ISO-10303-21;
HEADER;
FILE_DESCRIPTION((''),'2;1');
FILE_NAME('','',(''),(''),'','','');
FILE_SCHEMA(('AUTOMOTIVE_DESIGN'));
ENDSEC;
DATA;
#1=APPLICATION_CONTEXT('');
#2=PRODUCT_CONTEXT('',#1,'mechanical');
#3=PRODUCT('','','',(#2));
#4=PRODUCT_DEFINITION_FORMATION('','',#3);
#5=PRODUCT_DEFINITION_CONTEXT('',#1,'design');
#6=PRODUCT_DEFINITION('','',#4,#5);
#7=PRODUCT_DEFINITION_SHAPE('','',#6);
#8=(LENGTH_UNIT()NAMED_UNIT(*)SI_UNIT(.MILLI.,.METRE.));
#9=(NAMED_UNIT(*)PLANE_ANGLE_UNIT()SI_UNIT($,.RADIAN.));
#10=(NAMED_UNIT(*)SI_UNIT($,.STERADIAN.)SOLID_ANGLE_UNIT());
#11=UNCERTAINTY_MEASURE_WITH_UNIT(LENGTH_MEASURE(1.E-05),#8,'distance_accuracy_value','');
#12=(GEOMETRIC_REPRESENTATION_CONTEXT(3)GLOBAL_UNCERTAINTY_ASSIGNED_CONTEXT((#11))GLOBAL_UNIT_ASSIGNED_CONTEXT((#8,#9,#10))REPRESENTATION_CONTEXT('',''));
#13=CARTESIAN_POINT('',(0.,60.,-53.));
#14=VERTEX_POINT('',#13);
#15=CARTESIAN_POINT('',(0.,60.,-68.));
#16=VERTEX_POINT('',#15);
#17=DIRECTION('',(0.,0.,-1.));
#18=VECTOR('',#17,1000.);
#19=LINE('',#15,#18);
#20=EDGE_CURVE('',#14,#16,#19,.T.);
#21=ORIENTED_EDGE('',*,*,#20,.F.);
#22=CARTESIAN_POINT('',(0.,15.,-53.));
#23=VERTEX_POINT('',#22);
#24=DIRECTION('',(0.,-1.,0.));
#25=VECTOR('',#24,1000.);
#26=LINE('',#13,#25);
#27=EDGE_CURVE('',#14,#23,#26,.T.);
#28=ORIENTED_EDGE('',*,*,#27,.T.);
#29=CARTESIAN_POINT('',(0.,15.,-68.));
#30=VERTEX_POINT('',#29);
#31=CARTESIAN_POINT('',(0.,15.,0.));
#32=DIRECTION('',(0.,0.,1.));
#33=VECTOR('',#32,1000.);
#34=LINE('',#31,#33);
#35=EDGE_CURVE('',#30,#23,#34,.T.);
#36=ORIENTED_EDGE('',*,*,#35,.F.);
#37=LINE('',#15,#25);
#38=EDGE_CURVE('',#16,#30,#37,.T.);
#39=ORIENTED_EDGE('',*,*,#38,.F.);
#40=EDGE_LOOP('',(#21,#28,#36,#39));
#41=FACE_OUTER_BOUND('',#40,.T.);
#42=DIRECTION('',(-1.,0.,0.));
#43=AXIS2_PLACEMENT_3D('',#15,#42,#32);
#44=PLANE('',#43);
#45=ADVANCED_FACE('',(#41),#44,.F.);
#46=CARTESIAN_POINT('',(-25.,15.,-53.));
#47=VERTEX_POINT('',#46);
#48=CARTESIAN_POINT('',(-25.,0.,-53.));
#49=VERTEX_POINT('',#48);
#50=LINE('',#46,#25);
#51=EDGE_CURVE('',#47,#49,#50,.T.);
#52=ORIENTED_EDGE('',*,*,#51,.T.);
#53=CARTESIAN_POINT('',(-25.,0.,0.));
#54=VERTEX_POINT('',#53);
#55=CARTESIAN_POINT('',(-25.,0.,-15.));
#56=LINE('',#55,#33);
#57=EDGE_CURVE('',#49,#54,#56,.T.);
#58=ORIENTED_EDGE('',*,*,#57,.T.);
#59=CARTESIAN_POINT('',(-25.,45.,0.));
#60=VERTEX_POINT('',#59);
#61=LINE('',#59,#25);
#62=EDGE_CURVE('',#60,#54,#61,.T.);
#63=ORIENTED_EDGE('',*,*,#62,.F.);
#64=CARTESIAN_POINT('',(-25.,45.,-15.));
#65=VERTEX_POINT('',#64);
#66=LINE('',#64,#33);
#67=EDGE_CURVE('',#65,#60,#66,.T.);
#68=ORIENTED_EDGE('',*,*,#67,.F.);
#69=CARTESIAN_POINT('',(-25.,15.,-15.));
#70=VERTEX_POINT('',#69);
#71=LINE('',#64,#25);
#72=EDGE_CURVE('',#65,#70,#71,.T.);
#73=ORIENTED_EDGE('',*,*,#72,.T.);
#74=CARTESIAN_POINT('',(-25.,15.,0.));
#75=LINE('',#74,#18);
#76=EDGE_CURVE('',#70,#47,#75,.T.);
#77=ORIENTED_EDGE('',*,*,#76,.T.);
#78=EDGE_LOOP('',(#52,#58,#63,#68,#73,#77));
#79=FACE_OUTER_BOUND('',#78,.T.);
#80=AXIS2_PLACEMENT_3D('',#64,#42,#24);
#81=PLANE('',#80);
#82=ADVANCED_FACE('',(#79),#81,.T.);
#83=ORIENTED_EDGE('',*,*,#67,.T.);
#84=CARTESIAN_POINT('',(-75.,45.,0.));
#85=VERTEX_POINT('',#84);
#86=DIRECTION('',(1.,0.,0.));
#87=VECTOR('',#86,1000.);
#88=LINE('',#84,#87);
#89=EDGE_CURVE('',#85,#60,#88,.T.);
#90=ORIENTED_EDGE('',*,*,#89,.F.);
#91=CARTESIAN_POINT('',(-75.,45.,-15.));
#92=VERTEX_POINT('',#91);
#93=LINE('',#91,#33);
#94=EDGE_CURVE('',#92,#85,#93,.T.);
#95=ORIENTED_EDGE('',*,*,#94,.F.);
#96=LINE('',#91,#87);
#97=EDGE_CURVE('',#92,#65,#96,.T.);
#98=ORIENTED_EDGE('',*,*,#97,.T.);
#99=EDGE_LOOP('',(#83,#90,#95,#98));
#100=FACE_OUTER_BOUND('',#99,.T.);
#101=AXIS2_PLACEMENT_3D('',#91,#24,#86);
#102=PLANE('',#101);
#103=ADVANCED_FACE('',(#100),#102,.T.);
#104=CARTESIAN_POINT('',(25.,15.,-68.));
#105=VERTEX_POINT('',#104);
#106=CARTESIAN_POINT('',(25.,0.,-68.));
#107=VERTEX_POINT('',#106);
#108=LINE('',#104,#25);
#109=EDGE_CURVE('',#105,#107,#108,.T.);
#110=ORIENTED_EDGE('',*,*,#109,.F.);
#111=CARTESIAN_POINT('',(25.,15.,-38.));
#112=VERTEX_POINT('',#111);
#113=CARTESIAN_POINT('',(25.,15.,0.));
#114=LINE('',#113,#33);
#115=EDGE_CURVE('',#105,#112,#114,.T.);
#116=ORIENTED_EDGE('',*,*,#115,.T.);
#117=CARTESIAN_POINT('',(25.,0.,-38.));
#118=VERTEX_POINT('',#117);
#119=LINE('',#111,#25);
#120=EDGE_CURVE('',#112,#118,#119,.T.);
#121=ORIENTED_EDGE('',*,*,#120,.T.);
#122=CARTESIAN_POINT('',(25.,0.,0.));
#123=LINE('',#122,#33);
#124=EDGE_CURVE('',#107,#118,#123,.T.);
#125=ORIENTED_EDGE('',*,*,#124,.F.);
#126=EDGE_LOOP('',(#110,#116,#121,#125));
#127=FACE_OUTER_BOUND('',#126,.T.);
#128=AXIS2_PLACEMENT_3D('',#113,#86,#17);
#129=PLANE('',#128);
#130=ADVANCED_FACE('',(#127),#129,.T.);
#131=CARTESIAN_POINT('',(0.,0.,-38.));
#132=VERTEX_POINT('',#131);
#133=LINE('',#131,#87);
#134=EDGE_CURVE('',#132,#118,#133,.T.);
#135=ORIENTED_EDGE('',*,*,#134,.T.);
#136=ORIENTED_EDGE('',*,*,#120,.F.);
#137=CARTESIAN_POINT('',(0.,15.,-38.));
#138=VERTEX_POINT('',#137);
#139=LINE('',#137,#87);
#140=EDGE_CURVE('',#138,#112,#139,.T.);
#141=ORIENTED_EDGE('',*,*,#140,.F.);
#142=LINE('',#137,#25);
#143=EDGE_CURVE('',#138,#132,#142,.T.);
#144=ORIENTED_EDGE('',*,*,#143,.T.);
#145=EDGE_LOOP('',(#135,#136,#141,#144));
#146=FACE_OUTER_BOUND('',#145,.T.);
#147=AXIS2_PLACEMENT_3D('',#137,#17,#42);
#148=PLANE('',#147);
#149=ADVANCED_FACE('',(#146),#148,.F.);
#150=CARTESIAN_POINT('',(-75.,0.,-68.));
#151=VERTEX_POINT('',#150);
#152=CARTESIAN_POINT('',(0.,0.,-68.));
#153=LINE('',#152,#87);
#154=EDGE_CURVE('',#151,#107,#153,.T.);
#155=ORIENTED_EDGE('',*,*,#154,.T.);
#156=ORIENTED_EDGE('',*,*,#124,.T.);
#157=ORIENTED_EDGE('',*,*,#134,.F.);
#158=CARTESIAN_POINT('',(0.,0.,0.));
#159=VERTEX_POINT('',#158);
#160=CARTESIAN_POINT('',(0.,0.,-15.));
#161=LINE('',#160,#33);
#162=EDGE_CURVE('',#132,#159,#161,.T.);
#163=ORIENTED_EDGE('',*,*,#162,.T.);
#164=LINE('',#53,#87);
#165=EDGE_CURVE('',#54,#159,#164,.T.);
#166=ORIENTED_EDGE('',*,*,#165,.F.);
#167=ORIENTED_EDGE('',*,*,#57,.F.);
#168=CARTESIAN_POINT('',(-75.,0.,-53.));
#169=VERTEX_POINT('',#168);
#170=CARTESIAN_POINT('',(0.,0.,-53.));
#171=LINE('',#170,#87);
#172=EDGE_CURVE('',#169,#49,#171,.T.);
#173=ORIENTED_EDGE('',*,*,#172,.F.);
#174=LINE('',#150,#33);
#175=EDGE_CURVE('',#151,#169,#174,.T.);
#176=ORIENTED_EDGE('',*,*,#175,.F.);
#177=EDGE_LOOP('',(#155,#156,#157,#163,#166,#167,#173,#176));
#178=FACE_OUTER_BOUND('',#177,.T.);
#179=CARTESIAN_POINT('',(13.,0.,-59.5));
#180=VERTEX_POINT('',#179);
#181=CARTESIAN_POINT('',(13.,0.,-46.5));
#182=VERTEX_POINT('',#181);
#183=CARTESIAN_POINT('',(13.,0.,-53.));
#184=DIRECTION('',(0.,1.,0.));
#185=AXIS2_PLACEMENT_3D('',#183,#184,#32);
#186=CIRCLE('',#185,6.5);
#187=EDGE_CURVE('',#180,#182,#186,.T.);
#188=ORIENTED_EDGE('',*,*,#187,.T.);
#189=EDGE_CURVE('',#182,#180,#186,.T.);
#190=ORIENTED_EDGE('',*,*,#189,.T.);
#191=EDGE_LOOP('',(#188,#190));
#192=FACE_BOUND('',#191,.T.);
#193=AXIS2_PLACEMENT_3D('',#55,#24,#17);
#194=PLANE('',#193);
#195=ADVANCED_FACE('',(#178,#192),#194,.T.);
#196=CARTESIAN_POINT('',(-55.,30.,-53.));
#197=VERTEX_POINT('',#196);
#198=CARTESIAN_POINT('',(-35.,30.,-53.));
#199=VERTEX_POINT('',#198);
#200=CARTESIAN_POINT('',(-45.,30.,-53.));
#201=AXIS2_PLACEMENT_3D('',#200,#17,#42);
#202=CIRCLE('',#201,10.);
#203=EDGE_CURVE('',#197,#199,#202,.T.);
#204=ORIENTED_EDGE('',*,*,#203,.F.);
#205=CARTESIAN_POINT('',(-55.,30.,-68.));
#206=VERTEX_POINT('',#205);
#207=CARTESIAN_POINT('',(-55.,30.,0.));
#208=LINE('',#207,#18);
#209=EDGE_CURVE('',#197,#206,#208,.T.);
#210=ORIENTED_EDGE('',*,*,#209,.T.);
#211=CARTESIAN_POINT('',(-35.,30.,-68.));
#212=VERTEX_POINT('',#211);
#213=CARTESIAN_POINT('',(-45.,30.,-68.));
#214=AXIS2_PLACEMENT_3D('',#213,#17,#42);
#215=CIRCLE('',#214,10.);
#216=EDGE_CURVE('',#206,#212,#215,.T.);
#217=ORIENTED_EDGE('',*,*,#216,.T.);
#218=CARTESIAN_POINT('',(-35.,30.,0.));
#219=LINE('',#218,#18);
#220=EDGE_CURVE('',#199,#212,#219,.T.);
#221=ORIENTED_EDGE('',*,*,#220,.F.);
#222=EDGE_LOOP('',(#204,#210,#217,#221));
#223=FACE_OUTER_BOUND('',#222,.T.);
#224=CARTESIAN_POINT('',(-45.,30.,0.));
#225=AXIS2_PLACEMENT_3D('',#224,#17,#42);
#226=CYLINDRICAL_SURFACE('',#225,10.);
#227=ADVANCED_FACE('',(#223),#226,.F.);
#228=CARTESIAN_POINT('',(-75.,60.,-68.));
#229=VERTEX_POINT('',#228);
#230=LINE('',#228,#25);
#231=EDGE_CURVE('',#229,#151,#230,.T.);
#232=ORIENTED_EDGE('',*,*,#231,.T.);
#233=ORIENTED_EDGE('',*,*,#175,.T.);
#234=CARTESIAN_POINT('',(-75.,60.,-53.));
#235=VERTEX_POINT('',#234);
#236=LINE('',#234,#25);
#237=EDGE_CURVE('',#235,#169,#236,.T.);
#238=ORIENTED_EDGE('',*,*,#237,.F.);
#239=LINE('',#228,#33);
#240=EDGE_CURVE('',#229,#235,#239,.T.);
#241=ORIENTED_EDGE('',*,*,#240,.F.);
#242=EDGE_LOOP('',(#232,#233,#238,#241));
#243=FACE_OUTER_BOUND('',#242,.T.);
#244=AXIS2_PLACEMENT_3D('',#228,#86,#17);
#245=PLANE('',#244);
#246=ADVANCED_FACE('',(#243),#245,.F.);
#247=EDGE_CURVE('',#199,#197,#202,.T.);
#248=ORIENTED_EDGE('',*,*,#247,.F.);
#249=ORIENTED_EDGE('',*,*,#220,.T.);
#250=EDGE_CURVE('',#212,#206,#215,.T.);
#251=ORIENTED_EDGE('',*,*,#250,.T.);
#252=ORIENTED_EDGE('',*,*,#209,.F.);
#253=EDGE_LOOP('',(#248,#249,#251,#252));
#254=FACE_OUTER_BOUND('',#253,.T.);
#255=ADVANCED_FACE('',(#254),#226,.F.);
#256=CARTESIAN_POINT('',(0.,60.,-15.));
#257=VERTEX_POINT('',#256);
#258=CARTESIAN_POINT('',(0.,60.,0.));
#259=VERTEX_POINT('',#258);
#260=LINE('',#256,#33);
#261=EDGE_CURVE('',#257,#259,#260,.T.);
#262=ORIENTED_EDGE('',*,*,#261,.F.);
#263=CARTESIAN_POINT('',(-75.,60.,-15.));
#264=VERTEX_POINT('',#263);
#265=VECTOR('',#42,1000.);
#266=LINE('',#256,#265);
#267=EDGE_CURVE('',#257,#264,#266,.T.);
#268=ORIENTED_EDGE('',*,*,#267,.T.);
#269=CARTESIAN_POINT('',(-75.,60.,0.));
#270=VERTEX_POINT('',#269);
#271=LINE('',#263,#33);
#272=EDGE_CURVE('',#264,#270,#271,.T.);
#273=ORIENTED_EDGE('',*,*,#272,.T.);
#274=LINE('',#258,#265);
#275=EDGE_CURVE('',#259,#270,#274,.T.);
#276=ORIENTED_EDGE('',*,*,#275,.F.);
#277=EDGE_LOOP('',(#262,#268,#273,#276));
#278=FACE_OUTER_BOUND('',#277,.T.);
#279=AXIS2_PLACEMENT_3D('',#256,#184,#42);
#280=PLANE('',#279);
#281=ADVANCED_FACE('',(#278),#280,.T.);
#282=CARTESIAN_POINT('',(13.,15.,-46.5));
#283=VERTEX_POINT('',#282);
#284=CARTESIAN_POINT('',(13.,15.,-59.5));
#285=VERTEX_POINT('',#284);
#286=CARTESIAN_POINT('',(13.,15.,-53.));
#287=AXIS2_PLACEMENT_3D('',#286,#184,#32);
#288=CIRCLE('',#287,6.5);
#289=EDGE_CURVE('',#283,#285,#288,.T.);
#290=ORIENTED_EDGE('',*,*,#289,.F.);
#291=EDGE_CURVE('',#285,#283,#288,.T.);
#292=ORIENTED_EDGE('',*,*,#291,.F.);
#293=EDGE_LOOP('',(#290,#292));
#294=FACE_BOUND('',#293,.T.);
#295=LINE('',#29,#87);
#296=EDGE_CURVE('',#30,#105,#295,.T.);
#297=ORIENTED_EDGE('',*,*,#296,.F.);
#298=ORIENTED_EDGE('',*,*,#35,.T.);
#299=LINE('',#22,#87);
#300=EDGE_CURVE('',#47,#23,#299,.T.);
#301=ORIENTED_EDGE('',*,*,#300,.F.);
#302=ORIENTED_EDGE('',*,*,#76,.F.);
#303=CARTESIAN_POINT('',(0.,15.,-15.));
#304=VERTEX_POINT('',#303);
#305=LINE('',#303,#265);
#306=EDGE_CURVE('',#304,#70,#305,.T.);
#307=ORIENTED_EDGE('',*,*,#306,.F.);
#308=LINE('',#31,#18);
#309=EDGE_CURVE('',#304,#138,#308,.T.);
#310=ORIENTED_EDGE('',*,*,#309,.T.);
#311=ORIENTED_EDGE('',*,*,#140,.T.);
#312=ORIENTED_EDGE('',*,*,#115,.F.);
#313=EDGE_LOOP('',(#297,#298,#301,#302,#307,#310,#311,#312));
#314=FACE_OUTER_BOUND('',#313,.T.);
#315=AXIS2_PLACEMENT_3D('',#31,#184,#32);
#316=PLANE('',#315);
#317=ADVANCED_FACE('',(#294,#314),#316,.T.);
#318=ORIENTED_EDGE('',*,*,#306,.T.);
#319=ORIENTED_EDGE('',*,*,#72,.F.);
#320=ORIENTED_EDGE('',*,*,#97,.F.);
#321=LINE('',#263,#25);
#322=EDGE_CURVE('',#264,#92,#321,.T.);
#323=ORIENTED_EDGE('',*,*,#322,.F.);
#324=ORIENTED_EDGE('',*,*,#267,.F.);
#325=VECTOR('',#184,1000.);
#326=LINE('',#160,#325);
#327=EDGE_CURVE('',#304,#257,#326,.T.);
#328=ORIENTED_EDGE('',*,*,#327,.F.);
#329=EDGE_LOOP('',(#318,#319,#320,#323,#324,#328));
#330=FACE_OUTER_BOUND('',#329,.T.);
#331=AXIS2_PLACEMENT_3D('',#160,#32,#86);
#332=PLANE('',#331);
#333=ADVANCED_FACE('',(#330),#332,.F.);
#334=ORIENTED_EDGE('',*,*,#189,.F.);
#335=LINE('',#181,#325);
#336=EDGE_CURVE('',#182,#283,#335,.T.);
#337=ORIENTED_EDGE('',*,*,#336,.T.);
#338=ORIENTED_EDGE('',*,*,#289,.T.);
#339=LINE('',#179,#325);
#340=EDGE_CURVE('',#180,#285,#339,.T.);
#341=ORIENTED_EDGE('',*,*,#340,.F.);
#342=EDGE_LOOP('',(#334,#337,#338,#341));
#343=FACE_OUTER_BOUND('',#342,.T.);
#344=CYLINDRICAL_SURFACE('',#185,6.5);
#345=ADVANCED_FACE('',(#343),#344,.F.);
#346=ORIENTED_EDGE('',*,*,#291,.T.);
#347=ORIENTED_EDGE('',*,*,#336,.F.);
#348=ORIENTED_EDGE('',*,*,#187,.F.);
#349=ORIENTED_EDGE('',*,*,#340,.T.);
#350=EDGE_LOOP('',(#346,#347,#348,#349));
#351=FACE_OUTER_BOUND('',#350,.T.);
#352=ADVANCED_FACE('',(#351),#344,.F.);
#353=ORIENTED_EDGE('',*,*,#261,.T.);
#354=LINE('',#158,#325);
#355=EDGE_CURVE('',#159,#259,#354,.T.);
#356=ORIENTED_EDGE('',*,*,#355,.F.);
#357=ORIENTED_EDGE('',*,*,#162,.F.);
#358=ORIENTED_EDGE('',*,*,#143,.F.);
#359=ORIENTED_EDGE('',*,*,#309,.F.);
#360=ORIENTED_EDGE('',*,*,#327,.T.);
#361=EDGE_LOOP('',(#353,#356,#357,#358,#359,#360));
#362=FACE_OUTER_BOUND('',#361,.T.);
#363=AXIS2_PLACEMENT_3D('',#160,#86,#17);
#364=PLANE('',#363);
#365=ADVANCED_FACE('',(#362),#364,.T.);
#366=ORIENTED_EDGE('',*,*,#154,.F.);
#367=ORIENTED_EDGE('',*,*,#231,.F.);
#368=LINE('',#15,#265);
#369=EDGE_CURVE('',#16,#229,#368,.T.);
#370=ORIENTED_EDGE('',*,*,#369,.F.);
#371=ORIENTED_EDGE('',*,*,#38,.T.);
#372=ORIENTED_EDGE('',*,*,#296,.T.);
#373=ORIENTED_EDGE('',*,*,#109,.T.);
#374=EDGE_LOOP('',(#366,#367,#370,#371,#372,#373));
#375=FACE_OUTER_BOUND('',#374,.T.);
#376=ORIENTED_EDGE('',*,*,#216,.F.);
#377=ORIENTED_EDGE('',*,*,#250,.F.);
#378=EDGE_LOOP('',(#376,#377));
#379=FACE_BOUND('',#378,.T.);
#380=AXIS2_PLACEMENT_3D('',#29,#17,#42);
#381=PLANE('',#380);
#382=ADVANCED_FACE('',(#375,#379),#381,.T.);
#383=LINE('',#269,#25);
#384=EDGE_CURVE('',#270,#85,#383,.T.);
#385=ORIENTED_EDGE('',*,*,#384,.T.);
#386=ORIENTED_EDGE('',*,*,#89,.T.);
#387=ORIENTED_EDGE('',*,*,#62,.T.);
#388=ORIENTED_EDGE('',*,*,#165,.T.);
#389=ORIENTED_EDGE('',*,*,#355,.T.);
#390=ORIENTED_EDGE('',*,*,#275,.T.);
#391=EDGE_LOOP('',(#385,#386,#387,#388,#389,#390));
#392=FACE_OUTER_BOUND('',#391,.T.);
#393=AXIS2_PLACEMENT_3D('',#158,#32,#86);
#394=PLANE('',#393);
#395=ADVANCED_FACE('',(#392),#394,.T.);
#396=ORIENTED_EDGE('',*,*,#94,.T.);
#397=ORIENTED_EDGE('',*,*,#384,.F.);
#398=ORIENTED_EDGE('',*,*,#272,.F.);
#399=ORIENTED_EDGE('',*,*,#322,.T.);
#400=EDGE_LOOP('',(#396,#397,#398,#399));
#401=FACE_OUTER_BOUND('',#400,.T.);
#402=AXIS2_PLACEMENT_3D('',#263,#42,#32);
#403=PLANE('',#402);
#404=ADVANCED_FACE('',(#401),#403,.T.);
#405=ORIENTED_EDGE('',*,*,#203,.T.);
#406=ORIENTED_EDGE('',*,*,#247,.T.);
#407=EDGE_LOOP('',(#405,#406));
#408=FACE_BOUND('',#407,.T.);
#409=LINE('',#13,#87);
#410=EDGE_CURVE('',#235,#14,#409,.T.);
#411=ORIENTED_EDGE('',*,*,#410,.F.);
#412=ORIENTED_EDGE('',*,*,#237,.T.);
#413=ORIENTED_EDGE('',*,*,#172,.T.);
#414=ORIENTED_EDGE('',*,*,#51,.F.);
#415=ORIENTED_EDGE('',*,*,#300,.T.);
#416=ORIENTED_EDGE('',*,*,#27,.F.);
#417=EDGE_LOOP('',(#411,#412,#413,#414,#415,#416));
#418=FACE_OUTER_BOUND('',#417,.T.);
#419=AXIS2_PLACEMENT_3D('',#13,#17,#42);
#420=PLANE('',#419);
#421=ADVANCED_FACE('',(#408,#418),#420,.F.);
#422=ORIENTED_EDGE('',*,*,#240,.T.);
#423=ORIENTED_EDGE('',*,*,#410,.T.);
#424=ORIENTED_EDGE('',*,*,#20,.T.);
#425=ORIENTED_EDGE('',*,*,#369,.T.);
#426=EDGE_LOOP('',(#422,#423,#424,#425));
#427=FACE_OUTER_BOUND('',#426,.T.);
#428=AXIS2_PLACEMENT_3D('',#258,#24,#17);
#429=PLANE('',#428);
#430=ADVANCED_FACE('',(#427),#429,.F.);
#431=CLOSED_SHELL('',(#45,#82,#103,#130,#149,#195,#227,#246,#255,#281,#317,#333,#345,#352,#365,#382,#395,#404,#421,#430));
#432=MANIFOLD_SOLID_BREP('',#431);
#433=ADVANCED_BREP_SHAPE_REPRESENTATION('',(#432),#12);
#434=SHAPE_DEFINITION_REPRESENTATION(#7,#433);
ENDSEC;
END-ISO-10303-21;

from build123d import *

# Parameters (mm, degrees)
L_SIDE_WALL_DEPTH            = 15
BASE_FLANGE_WITH_TAB_DEPTH   = 15
UPRIGHT_PLATE_SKETCH_W       = 75
UPRIGHT_PLATE_SKETCH_H       = 15
UPRIGHT_PLATE_DEPTH          = 60
UPRIGHT_CROSS_HOLE_SKETCH_R  = 10
UPRIGHT_CROSS_HOLE_DEPTH     = 118.68177429
TAB_MOUNTING_HOLE_DEPTH      = 111.788086002
TAB_MOUNTING_HOLE_DEPTH_BACK = 111.788086002
TAB_MOUNTING_HOLE_SKETCH_R   = 6.5


with BuildPart() as part:
    # L Side Wall Sketch → L Side Wall (new body)
    with BuildSketch(Plane.XY):
        Polygon((0, 0), (0, 60), (-75, 60), (-75, 45), (-25, 45), (-25, 0), align=None)
    extrude(amount=-L_SIDE_WALL_DEPTH)

    # Base Flange Sketch → Base Flange With Tab (add)
    with BuildSketch(Plane(origin=(0, 0, 0), x_dir=(1, 0, 0), z_dir=(0, 1, 0))):
        Polygon((25, 68), (25, 38), (0, 38), (0, 0), (-25, 0), (-25, 53), (0, 53), (0, 68), align=None)
    extrude(amount=BASE_FLANGE_WITH_TAB_DEPTH)

    # Upright Plate Sketch → Upright Plate (add)
    with BuildSketch(Plane(origin=(0, 0, 0), x_dir=(1, 0, 0), z_dir=(0, 1, 0))):
        with Locations((-37.5, 60.5)):
            Rectangle(UPRIGHT_PLATE_SKETCH_W, UPRIGHT_PLATE_SKETCH_H)
    extrude(amount=UPRIGHT_PLATE_DEPTH)

    # Upright Cross Hole Sketch → Upright Cross Hole (cut, through all)
    with BuildSketch(Plane(origin=(0, 0, -68), x_dir=(-1, 0, 0), z_dir=(0, 0, -1))):
        with Locations((45, 30)):
            Circle(UPRIGHT_CROSS_HOLE_SKETCH_R)
    extrude(amount=-UPRIGHT_CROSS_HOLE_DEPTH, mode=Mode.SUBTRACT)

    # Tab Mounting Hole Sketch → Tab Mounting Hole (cut, two sides: drawn at the far end of the back side and taken through both)
    with BuildSketch(Plane(origin=(0, 15, 0), x_dir=(1, 0, 0), z_dir=(0, 1, 0)).offset(-TAB_MOUNTING_HOLE_DEPTH_BACK)):
        with Locations(Location((13, 53, 0), (0, 0, 270))):
            Circle(TAB_MOUNTING_HOLE_SKETCH_R)
    extrude(amount=TAB_MOUNTING_HOLE_DEPTH + TAB_MOUNTING_HOLE_DEPTH_BACK, mode=Mode.SUBTRACT)


solid = part.part
